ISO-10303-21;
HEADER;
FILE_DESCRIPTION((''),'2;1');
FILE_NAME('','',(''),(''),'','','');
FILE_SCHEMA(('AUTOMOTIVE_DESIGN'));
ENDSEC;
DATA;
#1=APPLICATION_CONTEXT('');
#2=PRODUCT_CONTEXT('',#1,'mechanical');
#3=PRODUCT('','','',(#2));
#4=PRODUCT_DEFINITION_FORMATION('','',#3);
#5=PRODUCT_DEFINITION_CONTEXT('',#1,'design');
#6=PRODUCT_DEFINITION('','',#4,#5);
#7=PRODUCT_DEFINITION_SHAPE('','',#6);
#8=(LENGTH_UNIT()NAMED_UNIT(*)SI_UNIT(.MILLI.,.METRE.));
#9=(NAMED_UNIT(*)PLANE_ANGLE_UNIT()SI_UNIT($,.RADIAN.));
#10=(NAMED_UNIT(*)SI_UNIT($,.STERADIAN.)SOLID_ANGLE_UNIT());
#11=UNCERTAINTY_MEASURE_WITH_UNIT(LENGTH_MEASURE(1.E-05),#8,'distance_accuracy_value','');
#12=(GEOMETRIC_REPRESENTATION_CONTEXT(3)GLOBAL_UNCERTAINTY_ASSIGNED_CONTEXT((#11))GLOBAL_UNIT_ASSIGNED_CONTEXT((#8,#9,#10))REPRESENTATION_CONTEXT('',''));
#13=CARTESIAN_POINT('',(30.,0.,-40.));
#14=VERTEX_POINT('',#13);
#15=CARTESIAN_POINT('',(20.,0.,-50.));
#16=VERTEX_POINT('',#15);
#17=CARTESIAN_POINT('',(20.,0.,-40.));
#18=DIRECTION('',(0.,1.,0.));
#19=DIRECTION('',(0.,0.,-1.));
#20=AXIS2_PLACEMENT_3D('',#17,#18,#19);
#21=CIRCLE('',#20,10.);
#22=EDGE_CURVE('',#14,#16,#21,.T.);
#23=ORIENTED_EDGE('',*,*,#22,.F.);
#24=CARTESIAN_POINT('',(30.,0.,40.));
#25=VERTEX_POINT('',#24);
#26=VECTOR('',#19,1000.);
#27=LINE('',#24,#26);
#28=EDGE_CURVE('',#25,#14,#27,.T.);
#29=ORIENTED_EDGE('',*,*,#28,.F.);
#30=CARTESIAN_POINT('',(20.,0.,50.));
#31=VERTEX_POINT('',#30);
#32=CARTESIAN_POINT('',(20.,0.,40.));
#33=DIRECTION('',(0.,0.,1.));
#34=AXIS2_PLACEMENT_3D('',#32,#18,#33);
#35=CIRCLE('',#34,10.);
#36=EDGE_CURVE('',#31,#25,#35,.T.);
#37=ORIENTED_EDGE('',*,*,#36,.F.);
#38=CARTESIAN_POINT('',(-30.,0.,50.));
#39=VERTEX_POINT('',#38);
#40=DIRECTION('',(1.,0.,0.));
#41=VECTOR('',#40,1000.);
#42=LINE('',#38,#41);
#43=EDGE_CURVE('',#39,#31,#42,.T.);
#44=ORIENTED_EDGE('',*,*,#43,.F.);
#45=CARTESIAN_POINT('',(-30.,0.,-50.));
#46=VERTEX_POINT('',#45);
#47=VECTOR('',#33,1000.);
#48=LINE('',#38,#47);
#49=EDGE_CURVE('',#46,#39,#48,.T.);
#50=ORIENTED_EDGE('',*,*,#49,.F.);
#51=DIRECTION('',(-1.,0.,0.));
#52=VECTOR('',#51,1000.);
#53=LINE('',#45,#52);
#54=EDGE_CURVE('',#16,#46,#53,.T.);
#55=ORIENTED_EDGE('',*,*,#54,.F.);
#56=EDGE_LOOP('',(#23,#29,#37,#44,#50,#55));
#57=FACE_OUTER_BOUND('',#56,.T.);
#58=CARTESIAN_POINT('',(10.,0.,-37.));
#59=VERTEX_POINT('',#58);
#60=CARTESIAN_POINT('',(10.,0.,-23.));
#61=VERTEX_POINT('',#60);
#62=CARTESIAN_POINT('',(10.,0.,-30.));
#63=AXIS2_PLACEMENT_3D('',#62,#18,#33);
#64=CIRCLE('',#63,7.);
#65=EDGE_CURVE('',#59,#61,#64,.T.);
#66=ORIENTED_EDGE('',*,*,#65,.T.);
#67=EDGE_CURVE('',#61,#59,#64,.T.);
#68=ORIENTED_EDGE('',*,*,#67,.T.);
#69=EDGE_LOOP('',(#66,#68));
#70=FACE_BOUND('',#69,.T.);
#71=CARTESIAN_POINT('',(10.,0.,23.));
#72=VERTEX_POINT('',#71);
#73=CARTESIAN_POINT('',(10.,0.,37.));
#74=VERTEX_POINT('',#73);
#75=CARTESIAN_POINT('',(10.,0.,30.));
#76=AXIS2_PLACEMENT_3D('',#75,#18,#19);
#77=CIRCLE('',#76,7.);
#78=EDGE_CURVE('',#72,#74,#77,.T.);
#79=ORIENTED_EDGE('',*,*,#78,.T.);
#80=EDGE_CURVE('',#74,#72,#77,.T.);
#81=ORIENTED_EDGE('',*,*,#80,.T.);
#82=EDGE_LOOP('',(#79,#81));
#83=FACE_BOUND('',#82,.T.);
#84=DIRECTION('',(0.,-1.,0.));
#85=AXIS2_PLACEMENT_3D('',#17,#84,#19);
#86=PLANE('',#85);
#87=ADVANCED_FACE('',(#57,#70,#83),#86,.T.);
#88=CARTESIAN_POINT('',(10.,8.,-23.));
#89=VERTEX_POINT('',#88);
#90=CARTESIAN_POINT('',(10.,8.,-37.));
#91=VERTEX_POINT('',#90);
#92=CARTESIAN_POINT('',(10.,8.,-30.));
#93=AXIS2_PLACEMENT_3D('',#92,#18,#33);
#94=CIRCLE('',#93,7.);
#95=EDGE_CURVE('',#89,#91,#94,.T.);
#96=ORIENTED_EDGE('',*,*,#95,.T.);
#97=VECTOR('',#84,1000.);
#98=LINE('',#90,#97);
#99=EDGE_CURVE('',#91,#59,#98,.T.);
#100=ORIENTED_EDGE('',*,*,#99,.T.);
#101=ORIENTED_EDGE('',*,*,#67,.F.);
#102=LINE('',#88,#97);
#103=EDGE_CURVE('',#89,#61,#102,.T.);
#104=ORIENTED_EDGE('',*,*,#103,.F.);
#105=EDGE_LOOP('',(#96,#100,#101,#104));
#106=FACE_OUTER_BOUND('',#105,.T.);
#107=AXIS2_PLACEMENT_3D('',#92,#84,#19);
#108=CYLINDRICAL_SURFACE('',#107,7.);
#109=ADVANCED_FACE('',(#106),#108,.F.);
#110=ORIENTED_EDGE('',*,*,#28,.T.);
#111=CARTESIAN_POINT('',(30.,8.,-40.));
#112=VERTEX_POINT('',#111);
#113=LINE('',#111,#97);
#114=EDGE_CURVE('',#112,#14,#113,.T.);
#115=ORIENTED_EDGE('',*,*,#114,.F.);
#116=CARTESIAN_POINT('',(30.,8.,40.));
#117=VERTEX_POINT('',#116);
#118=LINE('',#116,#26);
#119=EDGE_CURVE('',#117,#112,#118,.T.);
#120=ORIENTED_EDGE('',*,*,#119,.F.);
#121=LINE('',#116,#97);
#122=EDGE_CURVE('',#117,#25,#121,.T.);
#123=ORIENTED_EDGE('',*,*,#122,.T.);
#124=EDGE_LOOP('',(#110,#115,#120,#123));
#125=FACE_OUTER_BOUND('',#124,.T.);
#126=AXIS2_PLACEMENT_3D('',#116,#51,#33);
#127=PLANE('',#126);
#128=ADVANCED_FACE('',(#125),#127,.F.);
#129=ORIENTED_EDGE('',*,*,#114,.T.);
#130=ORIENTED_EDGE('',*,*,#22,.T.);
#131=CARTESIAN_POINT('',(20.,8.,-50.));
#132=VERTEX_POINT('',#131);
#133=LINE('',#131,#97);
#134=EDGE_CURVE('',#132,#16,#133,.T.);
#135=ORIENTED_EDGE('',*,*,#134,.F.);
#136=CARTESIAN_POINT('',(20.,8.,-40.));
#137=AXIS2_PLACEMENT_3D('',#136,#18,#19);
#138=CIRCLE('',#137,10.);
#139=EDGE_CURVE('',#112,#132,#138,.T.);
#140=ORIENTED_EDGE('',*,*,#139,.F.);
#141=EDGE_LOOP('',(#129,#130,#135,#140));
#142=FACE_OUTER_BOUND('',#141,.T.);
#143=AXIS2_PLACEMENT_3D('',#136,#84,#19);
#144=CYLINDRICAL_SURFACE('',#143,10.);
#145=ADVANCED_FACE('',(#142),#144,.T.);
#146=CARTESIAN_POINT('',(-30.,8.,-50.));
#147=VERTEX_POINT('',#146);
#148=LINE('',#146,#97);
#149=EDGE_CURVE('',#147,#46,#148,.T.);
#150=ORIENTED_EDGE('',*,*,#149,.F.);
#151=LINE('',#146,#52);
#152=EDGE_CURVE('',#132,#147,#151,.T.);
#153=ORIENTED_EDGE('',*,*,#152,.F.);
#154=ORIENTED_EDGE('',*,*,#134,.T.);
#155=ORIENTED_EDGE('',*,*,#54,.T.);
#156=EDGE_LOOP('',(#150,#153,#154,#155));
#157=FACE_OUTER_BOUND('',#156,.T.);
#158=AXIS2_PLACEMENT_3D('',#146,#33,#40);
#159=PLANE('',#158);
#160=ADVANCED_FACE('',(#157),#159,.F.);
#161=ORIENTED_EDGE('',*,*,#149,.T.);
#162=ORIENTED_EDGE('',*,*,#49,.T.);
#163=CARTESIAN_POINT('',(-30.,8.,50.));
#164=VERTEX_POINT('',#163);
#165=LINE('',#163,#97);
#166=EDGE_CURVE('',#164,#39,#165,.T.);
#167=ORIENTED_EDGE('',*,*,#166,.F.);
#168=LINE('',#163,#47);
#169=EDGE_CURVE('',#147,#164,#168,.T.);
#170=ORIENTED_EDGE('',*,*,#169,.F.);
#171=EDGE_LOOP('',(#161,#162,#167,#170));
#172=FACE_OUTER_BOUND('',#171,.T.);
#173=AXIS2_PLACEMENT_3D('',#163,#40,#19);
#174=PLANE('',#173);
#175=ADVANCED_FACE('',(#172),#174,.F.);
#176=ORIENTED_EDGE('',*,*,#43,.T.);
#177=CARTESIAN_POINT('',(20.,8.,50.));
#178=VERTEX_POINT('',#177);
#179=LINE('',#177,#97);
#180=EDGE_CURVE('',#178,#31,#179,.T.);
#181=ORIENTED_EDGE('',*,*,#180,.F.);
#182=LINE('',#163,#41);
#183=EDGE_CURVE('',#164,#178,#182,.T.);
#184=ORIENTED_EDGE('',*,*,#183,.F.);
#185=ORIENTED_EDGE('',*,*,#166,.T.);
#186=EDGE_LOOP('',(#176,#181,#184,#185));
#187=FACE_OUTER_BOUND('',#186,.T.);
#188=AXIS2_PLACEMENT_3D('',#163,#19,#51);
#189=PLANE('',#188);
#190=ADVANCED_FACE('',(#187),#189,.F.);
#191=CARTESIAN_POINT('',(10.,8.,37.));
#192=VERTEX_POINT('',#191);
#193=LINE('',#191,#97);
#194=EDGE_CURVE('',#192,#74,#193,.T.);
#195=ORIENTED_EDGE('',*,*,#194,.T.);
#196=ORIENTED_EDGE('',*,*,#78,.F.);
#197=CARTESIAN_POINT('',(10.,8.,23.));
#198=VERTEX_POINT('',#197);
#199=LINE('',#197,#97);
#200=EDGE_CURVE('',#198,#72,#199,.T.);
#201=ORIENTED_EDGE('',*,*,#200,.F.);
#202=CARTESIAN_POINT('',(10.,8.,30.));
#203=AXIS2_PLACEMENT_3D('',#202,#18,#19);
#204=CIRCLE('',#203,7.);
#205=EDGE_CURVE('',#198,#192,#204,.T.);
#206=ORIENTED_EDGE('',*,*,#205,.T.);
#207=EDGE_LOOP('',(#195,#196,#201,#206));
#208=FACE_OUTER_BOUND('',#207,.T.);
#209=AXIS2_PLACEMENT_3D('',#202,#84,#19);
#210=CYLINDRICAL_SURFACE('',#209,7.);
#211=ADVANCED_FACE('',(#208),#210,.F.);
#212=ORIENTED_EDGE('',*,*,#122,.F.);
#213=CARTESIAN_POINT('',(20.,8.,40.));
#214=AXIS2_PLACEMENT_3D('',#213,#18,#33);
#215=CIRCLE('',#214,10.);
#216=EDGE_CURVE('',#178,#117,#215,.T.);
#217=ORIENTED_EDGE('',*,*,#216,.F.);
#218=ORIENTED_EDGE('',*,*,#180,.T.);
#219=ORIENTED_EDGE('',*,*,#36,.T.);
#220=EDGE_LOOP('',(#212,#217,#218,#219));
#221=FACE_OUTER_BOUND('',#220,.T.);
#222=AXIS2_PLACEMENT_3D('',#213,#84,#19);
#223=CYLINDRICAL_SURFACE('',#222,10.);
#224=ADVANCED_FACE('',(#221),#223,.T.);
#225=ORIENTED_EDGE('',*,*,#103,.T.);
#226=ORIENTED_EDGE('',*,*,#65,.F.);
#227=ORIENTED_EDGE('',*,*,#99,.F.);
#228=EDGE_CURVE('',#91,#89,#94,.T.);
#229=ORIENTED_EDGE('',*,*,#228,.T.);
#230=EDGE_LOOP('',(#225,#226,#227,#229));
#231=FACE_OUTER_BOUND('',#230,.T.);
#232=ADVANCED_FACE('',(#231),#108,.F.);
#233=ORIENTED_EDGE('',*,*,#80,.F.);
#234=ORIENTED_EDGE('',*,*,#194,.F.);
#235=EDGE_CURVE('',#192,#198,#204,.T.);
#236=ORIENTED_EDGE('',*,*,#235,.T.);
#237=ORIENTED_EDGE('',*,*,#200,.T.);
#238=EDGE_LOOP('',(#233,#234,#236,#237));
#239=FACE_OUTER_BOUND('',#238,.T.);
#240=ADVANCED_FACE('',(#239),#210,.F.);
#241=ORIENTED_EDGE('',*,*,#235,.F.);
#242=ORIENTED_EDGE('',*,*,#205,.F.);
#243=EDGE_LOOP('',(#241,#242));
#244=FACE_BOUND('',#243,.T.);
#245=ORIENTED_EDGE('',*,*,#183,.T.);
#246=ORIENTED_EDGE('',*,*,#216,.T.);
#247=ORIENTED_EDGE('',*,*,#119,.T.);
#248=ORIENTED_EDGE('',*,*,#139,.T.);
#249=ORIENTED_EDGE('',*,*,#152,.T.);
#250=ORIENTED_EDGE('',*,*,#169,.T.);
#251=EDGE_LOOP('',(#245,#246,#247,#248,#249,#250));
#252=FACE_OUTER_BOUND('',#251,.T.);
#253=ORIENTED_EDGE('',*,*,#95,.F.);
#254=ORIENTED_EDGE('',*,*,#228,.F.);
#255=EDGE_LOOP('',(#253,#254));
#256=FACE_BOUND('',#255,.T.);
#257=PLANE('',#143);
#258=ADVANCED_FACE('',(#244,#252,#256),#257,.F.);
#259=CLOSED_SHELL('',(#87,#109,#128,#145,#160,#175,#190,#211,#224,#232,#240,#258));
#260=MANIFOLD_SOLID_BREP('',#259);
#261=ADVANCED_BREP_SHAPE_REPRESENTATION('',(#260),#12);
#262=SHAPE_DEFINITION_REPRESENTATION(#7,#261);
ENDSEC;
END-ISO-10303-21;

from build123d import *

# Parameters (mm, degrees)
SKETCH1_R           = 7
BOSS_EXTRUDE1_DEPTH = 8


with BuildPart() as part:
    # Sketch1 → Boss-Extrude1 (new body)
    with BuildSketch(Plane(origin=(0, 0, 0), x_dir=(1, 0, 0), z_dir=(0, 1, 0))):
        with BuildLine():
            Line((-30, -50), (20, -50))
            ThreePointArc((20, -50), (27.071067812, -47.071067812), (30, -40))
            Line((30, -40), (30, 40))
            ThreePointArc((30, 40), (27.071067812, 47.071067812), (20, 50))
            Line((20, 50), (-30, 50))
            Line((-30, 50), (-30, -50))
        make_face()
        with Locations(Location((10, 30, 0), (0, 0, 270))):
            Circle(SKETCH1_R, mode=Mode.SUBTRACT)
        with Locations(Location((10, -30, 0), (0, 0, 90))):
            Circle(SKETCH1_R, mode=Mode.SUBTRACT)
    extrude(amount=BOSS_EXTRUDE1_DEPTH)


solid = part.part
